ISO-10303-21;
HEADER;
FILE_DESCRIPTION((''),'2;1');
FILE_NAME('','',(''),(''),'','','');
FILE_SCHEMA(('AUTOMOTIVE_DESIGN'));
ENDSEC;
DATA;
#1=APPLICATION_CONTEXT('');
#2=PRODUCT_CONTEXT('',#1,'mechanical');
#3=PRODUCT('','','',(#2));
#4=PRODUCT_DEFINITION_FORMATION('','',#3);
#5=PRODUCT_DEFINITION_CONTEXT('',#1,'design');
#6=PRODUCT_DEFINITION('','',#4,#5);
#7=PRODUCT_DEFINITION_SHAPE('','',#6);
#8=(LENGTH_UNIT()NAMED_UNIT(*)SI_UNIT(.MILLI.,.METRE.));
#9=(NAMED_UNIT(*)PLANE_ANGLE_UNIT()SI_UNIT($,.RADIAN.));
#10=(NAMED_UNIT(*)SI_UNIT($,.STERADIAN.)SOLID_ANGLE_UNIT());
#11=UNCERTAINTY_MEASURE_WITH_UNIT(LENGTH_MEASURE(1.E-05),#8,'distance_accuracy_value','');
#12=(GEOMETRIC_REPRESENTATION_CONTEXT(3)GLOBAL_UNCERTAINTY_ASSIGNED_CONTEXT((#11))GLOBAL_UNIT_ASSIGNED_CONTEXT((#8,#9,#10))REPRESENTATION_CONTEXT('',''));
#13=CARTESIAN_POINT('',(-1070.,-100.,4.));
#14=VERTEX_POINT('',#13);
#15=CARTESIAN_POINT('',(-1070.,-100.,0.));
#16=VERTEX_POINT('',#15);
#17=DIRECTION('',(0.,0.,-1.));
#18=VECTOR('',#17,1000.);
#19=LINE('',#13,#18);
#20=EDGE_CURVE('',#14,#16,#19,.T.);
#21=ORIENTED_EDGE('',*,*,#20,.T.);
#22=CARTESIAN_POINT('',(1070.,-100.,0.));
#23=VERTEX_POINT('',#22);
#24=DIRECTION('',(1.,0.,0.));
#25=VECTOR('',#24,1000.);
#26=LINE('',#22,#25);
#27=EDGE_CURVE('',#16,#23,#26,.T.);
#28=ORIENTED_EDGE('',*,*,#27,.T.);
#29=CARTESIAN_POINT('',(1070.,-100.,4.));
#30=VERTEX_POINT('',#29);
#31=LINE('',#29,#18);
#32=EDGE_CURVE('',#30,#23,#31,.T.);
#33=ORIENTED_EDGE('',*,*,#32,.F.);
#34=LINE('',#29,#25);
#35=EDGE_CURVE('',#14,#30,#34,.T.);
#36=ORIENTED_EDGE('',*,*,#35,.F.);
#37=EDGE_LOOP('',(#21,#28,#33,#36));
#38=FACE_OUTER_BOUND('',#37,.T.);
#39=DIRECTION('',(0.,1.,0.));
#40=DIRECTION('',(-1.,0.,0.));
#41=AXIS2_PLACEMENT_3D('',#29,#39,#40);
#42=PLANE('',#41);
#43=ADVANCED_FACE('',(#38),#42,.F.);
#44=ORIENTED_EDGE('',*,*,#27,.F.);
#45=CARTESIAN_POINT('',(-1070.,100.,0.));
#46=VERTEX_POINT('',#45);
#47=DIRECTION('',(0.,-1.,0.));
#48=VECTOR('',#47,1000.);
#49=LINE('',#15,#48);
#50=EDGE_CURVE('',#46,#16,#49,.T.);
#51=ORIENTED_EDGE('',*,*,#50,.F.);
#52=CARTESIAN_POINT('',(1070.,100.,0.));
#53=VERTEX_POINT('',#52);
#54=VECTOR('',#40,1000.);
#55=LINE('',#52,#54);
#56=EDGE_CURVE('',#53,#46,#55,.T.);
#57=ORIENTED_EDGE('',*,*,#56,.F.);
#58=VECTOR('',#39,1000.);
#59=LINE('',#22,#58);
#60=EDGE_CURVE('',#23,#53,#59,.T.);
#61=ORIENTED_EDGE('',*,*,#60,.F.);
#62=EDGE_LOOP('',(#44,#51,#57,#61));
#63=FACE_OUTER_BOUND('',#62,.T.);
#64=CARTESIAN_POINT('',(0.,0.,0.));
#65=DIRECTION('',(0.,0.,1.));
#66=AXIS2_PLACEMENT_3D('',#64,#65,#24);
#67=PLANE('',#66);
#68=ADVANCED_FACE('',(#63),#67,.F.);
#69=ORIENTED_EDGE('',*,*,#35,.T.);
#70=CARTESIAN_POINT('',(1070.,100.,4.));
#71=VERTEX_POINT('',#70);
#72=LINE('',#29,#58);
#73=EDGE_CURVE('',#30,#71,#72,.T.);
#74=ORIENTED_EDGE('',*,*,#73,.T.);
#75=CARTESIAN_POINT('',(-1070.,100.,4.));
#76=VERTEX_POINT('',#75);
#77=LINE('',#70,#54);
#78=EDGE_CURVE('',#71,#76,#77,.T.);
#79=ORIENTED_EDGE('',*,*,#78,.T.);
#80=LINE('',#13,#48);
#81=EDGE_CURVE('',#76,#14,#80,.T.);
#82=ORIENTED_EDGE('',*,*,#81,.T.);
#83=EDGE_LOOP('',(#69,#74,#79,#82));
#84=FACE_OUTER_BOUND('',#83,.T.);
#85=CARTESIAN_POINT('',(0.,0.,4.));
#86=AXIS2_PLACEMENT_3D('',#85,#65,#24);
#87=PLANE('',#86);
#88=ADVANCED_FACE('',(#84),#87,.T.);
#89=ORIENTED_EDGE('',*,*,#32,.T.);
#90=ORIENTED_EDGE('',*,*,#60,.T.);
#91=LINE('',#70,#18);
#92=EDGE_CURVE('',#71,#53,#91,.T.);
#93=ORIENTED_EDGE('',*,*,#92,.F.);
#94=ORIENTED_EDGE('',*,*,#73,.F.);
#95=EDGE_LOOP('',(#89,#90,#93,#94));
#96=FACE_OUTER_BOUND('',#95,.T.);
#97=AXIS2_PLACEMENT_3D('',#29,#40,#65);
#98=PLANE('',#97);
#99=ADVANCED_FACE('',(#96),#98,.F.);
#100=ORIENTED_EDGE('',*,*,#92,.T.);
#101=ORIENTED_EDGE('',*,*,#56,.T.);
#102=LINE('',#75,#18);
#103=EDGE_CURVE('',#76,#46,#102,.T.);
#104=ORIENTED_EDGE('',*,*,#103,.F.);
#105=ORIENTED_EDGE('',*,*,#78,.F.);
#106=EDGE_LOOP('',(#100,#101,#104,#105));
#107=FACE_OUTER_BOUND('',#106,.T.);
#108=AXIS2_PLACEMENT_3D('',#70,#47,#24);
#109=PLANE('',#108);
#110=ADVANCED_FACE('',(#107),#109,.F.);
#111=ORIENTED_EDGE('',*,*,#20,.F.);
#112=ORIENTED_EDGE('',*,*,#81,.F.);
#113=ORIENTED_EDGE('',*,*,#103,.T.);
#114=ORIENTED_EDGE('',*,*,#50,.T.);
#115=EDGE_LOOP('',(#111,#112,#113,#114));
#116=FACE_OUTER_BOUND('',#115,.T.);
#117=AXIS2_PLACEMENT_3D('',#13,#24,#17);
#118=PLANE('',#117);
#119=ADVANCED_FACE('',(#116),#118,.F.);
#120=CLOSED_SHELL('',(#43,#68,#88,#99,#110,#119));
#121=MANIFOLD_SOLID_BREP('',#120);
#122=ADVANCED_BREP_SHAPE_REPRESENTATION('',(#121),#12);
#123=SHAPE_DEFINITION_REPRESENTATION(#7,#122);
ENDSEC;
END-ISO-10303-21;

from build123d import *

# Parameters (mm, degrees)
SKETCH_1_W      = 2140
SKETCH_1_H      = 200
EXTRUDE_1_DEPTH = 4


with BuildPart() as part:
    # 草图1 → 凸台-拉伸1 (new body)
    with BuildSketch(Plane.XY):
        Rectangle(SKETCH_1_W, SKETCH_1_H)
    extrude(amount=EXTRUDE_1_DEPTH)


solid = part.part
